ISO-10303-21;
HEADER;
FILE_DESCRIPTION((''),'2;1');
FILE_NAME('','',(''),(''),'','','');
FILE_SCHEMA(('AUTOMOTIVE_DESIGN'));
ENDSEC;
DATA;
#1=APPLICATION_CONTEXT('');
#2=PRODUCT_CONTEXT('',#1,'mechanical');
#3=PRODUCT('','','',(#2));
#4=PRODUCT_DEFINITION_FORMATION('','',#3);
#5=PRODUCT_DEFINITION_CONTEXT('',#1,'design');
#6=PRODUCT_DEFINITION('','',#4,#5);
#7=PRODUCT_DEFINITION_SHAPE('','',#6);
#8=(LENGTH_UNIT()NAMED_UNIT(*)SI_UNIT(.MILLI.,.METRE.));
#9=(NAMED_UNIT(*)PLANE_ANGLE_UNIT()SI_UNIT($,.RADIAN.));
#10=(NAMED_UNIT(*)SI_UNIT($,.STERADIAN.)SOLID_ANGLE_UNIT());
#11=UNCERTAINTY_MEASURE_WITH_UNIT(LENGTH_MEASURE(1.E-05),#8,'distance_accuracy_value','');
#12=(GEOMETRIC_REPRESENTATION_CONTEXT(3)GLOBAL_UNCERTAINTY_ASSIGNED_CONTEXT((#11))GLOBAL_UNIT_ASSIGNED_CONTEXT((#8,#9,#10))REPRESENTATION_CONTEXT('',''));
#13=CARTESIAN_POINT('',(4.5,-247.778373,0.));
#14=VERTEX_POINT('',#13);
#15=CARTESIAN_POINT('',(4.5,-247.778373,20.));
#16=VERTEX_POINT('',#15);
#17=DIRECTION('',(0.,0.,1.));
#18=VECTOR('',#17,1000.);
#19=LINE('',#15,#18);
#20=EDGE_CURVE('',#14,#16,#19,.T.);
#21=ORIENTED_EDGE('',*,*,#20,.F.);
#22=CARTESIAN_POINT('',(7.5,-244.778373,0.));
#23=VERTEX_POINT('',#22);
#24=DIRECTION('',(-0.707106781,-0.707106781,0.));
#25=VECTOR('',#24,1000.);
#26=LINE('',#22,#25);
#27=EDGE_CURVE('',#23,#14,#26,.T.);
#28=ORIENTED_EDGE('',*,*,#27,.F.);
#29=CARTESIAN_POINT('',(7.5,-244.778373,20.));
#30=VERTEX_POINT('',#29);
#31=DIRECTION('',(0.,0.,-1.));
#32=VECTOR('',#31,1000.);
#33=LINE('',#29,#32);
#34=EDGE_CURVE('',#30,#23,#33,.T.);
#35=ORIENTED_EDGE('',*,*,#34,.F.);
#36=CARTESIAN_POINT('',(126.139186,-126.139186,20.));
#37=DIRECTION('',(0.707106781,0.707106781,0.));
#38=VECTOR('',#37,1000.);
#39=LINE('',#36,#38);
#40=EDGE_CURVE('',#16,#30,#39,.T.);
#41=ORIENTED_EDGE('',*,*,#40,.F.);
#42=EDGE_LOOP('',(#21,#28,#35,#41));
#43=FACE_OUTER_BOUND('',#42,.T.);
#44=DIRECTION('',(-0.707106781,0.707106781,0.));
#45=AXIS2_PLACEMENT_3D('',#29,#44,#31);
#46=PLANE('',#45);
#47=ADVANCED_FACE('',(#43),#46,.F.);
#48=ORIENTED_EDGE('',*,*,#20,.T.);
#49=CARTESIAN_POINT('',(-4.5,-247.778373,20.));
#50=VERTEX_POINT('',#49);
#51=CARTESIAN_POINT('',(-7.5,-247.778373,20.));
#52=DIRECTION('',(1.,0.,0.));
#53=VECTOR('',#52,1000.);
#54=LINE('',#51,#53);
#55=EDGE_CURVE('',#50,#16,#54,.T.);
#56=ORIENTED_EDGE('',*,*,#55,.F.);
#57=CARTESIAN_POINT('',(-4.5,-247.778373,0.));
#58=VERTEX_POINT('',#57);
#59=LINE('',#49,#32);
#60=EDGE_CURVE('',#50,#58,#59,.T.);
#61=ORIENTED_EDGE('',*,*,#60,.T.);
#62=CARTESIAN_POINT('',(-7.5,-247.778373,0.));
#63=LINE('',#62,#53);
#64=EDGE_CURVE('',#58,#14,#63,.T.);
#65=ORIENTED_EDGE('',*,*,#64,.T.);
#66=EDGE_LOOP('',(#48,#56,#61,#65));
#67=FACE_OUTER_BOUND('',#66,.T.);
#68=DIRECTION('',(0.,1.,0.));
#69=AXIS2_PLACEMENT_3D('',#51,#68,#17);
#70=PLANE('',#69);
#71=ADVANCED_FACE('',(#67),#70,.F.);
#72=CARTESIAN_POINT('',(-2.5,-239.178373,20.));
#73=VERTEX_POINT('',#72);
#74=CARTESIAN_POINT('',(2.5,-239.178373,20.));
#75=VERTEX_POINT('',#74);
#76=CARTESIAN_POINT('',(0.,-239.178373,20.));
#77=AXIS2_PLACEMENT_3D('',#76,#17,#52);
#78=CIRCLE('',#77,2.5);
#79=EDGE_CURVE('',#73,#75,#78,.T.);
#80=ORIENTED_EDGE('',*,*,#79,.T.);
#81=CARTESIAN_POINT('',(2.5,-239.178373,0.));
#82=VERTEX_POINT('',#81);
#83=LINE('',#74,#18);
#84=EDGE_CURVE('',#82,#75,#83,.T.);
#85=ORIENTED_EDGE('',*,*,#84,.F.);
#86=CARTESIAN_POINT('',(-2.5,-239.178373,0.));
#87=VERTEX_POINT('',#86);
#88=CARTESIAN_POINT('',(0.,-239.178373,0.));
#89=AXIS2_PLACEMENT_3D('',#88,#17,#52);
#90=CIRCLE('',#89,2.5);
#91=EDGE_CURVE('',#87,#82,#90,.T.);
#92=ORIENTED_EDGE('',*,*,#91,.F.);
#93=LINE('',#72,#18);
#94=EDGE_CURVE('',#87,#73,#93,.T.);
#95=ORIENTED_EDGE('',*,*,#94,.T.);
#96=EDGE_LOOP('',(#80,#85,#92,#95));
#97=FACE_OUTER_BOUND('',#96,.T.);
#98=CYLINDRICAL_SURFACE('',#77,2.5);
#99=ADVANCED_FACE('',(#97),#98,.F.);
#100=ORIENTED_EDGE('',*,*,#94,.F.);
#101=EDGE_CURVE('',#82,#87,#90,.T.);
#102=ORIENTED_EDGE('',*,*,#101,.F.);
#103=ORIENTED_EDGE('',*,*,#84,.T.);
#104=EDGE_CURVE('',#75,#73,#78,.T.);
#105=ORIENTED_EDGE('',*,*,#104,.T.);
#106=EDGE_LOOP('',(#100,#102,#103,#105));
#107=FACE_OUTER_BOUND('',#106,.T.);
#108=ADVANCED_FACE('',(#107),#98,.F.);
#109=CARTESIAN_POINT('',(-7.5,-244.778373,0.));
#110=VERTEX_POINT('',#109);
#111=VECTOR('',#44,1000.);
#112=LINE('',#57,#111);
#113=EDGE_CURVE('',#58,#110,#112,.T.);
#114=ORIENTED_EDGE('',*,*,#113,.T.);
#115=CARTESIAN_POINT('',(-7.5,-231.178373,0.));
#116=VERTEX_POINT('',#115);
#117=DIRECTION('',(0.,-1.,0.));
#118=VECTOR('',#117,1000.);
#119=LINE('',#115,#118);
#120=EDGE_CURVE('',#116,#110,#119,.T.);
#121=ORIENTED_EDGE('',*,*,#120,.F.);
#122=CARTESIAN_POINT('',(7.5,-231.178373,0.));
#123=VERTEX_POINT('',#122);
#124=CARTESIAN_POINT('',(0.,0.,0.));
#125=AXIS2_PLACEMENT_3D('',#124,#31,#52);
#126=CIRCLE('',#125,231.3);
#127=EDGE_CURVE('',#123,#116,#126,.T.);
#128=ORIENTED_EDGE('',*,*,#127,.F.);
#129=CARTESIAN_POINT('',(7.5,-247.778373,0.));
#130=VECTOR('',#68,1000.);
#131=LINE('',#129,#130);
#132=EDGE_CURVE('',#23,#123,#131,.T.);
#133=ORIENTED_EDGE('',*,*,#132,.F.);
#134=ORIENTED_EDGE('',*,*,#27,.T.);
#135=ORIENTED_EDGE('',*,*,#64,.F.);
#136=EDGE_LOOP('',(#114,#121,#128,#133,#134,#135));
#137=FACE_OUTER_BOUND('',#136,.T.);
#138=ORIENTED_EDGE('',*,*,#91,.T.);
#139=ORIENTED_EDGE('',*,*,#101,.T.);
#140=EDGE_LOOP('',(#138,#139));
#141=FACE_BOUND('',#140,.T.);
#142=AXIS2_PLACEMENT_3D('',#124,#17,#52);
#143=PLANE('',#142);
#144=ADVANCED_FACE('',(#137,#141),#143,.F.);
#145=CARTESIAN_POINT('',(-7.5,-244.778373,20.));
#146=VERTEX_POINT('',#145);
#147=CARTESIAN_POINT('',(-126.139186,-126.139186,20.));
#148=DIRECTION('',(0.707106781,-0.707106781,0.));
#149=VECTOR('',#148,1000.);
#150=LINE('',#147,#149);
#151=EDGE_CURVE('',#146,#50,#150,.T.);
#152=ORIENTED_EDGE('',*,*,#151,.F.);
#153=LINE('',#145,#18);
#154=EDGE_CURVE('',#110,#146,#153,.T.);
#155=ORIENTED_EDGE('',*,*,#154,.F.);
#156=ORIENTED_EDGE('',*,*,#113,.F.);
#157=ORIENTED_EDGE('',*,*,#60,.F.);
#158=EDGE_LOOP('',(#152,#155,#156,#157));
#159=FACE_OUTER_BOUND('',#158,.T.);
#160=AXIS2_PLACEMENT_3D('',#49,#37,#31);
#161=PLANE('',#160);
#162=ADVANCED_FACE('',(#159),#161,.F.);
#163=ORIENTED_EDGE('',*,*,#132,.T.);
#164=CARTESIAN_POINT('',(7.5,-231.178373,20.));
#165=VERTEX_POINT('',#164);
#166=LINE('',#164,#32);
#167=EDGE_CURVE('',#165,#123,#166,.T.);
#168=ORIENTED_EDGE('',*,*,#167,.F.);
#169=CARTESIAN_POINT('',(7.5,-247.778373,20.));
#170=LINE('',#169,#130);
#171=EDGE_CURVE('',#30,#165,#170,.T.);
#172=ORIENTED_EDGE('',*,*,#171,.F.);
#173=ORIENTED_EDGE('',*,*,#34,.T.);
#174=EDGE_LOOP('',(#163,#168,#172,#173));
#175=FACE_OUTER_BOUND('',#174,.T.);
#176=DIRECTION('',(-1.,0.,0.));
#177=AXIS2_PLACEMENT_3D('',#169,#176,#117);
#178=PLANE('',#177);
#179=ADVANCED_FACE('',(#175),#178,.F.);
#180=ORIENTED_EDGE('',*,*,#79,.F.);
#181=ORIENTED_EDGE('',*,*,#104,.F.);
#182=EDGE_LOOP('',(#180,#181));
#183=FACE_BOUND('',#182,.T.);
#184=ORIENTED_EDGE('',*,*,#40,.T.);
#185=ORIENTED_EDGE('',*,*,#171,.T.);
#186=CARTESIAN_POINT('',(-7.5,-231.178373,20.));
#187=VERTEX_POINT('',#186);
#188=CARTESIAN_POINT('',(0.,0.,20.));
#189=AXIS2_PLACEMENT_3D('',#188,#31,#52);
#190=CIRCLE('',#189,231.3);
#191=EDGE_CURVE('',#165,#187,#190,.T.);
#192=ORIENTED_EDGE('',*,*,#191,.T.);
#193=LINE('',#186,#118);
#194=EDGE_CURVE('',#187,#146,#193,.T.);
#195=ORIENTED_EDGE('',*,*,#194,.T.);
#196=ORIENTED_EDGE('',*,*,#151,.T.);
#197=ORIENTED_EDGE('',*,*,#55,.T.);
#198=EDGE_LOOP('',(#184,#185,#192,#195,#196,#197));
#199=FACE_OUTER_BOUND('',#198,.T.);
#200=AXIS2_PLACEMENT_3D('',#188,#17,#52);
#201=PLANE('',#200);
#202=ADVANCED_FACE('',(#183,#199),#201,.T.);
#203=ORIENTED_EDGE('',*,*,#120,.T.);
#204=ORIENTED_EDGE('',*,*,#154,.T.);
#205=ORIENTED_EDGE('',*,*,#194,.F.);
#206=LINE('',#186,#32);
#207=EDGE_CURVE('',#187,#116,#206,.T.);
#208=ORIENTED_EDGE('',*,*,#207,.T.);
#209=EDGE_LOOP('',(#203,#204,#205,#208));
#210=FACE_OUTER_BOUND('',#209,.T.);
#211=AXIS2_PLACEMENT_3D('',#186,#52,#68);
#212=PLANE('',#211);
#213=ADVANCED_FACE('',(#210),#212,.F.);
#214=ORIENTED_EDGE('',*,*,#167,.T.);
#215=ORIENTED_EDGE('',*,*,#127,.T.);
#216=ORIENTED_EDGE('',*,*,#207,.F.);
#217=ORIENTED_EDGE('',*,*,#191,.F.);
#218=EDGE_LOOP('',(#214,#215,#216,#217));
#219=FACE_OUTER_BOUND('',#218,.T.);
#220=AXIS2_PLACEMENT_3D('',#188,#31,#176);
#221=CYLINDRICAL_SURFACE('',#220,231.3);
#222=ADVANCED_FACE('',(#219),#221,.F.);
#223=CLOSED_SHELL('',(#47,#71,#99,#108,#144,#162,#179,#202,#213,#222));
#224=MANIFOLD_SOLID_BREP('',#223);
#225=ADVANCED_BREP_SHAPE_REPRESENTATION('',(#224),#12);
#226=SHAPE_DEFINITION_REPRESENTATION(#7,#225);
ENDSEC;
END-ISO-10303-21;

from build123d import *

# Parameters (mm, degrees)
BOSS_EXTRUDE1_DEPTH = 20
CHAMFER1_SIZE       = 3
M6_TAPPED_HOLE1_D   = 5


with BuildPart() as part:
    # Sketch1 → Boss-Extrude1 (new body)
    with BuildSketch(Plane.XY):
        with BuildLine():
            Line((-7.5, -231.178372691), (-7.5, -247.778372691))
            Line((-7.5, -247.778372691), (7.5, -247.778372691))
            Line((7.5, -247.778372691), (7.5, -231.178372691))
            ThreePointArc((7.5, -231.178372691), (0, -231.3), (-7.5, -231.178372691))
        make_face()
    extrude(amount=BOSS_EXTRUDE1_DEPTH)

    # Chamfer1
    chamfer1_edges = [part.edges().sort_by_distance(p)[0] for p in [
        (7.5, -247.778372691, 10),
        (-7.5, -247.778372691, 10),
    ]]
    chamfer(chamfer1_edges, length=CHAMFER1_SIZE)

    # M6 Tapped Hole1 (through all)
    with Locations(Plane.XY.offset(20)):
        with Locations((0, -239.178372691)):
            Hole(M6_TAPPED_HOLE1_D / 2)


solid = part.part
